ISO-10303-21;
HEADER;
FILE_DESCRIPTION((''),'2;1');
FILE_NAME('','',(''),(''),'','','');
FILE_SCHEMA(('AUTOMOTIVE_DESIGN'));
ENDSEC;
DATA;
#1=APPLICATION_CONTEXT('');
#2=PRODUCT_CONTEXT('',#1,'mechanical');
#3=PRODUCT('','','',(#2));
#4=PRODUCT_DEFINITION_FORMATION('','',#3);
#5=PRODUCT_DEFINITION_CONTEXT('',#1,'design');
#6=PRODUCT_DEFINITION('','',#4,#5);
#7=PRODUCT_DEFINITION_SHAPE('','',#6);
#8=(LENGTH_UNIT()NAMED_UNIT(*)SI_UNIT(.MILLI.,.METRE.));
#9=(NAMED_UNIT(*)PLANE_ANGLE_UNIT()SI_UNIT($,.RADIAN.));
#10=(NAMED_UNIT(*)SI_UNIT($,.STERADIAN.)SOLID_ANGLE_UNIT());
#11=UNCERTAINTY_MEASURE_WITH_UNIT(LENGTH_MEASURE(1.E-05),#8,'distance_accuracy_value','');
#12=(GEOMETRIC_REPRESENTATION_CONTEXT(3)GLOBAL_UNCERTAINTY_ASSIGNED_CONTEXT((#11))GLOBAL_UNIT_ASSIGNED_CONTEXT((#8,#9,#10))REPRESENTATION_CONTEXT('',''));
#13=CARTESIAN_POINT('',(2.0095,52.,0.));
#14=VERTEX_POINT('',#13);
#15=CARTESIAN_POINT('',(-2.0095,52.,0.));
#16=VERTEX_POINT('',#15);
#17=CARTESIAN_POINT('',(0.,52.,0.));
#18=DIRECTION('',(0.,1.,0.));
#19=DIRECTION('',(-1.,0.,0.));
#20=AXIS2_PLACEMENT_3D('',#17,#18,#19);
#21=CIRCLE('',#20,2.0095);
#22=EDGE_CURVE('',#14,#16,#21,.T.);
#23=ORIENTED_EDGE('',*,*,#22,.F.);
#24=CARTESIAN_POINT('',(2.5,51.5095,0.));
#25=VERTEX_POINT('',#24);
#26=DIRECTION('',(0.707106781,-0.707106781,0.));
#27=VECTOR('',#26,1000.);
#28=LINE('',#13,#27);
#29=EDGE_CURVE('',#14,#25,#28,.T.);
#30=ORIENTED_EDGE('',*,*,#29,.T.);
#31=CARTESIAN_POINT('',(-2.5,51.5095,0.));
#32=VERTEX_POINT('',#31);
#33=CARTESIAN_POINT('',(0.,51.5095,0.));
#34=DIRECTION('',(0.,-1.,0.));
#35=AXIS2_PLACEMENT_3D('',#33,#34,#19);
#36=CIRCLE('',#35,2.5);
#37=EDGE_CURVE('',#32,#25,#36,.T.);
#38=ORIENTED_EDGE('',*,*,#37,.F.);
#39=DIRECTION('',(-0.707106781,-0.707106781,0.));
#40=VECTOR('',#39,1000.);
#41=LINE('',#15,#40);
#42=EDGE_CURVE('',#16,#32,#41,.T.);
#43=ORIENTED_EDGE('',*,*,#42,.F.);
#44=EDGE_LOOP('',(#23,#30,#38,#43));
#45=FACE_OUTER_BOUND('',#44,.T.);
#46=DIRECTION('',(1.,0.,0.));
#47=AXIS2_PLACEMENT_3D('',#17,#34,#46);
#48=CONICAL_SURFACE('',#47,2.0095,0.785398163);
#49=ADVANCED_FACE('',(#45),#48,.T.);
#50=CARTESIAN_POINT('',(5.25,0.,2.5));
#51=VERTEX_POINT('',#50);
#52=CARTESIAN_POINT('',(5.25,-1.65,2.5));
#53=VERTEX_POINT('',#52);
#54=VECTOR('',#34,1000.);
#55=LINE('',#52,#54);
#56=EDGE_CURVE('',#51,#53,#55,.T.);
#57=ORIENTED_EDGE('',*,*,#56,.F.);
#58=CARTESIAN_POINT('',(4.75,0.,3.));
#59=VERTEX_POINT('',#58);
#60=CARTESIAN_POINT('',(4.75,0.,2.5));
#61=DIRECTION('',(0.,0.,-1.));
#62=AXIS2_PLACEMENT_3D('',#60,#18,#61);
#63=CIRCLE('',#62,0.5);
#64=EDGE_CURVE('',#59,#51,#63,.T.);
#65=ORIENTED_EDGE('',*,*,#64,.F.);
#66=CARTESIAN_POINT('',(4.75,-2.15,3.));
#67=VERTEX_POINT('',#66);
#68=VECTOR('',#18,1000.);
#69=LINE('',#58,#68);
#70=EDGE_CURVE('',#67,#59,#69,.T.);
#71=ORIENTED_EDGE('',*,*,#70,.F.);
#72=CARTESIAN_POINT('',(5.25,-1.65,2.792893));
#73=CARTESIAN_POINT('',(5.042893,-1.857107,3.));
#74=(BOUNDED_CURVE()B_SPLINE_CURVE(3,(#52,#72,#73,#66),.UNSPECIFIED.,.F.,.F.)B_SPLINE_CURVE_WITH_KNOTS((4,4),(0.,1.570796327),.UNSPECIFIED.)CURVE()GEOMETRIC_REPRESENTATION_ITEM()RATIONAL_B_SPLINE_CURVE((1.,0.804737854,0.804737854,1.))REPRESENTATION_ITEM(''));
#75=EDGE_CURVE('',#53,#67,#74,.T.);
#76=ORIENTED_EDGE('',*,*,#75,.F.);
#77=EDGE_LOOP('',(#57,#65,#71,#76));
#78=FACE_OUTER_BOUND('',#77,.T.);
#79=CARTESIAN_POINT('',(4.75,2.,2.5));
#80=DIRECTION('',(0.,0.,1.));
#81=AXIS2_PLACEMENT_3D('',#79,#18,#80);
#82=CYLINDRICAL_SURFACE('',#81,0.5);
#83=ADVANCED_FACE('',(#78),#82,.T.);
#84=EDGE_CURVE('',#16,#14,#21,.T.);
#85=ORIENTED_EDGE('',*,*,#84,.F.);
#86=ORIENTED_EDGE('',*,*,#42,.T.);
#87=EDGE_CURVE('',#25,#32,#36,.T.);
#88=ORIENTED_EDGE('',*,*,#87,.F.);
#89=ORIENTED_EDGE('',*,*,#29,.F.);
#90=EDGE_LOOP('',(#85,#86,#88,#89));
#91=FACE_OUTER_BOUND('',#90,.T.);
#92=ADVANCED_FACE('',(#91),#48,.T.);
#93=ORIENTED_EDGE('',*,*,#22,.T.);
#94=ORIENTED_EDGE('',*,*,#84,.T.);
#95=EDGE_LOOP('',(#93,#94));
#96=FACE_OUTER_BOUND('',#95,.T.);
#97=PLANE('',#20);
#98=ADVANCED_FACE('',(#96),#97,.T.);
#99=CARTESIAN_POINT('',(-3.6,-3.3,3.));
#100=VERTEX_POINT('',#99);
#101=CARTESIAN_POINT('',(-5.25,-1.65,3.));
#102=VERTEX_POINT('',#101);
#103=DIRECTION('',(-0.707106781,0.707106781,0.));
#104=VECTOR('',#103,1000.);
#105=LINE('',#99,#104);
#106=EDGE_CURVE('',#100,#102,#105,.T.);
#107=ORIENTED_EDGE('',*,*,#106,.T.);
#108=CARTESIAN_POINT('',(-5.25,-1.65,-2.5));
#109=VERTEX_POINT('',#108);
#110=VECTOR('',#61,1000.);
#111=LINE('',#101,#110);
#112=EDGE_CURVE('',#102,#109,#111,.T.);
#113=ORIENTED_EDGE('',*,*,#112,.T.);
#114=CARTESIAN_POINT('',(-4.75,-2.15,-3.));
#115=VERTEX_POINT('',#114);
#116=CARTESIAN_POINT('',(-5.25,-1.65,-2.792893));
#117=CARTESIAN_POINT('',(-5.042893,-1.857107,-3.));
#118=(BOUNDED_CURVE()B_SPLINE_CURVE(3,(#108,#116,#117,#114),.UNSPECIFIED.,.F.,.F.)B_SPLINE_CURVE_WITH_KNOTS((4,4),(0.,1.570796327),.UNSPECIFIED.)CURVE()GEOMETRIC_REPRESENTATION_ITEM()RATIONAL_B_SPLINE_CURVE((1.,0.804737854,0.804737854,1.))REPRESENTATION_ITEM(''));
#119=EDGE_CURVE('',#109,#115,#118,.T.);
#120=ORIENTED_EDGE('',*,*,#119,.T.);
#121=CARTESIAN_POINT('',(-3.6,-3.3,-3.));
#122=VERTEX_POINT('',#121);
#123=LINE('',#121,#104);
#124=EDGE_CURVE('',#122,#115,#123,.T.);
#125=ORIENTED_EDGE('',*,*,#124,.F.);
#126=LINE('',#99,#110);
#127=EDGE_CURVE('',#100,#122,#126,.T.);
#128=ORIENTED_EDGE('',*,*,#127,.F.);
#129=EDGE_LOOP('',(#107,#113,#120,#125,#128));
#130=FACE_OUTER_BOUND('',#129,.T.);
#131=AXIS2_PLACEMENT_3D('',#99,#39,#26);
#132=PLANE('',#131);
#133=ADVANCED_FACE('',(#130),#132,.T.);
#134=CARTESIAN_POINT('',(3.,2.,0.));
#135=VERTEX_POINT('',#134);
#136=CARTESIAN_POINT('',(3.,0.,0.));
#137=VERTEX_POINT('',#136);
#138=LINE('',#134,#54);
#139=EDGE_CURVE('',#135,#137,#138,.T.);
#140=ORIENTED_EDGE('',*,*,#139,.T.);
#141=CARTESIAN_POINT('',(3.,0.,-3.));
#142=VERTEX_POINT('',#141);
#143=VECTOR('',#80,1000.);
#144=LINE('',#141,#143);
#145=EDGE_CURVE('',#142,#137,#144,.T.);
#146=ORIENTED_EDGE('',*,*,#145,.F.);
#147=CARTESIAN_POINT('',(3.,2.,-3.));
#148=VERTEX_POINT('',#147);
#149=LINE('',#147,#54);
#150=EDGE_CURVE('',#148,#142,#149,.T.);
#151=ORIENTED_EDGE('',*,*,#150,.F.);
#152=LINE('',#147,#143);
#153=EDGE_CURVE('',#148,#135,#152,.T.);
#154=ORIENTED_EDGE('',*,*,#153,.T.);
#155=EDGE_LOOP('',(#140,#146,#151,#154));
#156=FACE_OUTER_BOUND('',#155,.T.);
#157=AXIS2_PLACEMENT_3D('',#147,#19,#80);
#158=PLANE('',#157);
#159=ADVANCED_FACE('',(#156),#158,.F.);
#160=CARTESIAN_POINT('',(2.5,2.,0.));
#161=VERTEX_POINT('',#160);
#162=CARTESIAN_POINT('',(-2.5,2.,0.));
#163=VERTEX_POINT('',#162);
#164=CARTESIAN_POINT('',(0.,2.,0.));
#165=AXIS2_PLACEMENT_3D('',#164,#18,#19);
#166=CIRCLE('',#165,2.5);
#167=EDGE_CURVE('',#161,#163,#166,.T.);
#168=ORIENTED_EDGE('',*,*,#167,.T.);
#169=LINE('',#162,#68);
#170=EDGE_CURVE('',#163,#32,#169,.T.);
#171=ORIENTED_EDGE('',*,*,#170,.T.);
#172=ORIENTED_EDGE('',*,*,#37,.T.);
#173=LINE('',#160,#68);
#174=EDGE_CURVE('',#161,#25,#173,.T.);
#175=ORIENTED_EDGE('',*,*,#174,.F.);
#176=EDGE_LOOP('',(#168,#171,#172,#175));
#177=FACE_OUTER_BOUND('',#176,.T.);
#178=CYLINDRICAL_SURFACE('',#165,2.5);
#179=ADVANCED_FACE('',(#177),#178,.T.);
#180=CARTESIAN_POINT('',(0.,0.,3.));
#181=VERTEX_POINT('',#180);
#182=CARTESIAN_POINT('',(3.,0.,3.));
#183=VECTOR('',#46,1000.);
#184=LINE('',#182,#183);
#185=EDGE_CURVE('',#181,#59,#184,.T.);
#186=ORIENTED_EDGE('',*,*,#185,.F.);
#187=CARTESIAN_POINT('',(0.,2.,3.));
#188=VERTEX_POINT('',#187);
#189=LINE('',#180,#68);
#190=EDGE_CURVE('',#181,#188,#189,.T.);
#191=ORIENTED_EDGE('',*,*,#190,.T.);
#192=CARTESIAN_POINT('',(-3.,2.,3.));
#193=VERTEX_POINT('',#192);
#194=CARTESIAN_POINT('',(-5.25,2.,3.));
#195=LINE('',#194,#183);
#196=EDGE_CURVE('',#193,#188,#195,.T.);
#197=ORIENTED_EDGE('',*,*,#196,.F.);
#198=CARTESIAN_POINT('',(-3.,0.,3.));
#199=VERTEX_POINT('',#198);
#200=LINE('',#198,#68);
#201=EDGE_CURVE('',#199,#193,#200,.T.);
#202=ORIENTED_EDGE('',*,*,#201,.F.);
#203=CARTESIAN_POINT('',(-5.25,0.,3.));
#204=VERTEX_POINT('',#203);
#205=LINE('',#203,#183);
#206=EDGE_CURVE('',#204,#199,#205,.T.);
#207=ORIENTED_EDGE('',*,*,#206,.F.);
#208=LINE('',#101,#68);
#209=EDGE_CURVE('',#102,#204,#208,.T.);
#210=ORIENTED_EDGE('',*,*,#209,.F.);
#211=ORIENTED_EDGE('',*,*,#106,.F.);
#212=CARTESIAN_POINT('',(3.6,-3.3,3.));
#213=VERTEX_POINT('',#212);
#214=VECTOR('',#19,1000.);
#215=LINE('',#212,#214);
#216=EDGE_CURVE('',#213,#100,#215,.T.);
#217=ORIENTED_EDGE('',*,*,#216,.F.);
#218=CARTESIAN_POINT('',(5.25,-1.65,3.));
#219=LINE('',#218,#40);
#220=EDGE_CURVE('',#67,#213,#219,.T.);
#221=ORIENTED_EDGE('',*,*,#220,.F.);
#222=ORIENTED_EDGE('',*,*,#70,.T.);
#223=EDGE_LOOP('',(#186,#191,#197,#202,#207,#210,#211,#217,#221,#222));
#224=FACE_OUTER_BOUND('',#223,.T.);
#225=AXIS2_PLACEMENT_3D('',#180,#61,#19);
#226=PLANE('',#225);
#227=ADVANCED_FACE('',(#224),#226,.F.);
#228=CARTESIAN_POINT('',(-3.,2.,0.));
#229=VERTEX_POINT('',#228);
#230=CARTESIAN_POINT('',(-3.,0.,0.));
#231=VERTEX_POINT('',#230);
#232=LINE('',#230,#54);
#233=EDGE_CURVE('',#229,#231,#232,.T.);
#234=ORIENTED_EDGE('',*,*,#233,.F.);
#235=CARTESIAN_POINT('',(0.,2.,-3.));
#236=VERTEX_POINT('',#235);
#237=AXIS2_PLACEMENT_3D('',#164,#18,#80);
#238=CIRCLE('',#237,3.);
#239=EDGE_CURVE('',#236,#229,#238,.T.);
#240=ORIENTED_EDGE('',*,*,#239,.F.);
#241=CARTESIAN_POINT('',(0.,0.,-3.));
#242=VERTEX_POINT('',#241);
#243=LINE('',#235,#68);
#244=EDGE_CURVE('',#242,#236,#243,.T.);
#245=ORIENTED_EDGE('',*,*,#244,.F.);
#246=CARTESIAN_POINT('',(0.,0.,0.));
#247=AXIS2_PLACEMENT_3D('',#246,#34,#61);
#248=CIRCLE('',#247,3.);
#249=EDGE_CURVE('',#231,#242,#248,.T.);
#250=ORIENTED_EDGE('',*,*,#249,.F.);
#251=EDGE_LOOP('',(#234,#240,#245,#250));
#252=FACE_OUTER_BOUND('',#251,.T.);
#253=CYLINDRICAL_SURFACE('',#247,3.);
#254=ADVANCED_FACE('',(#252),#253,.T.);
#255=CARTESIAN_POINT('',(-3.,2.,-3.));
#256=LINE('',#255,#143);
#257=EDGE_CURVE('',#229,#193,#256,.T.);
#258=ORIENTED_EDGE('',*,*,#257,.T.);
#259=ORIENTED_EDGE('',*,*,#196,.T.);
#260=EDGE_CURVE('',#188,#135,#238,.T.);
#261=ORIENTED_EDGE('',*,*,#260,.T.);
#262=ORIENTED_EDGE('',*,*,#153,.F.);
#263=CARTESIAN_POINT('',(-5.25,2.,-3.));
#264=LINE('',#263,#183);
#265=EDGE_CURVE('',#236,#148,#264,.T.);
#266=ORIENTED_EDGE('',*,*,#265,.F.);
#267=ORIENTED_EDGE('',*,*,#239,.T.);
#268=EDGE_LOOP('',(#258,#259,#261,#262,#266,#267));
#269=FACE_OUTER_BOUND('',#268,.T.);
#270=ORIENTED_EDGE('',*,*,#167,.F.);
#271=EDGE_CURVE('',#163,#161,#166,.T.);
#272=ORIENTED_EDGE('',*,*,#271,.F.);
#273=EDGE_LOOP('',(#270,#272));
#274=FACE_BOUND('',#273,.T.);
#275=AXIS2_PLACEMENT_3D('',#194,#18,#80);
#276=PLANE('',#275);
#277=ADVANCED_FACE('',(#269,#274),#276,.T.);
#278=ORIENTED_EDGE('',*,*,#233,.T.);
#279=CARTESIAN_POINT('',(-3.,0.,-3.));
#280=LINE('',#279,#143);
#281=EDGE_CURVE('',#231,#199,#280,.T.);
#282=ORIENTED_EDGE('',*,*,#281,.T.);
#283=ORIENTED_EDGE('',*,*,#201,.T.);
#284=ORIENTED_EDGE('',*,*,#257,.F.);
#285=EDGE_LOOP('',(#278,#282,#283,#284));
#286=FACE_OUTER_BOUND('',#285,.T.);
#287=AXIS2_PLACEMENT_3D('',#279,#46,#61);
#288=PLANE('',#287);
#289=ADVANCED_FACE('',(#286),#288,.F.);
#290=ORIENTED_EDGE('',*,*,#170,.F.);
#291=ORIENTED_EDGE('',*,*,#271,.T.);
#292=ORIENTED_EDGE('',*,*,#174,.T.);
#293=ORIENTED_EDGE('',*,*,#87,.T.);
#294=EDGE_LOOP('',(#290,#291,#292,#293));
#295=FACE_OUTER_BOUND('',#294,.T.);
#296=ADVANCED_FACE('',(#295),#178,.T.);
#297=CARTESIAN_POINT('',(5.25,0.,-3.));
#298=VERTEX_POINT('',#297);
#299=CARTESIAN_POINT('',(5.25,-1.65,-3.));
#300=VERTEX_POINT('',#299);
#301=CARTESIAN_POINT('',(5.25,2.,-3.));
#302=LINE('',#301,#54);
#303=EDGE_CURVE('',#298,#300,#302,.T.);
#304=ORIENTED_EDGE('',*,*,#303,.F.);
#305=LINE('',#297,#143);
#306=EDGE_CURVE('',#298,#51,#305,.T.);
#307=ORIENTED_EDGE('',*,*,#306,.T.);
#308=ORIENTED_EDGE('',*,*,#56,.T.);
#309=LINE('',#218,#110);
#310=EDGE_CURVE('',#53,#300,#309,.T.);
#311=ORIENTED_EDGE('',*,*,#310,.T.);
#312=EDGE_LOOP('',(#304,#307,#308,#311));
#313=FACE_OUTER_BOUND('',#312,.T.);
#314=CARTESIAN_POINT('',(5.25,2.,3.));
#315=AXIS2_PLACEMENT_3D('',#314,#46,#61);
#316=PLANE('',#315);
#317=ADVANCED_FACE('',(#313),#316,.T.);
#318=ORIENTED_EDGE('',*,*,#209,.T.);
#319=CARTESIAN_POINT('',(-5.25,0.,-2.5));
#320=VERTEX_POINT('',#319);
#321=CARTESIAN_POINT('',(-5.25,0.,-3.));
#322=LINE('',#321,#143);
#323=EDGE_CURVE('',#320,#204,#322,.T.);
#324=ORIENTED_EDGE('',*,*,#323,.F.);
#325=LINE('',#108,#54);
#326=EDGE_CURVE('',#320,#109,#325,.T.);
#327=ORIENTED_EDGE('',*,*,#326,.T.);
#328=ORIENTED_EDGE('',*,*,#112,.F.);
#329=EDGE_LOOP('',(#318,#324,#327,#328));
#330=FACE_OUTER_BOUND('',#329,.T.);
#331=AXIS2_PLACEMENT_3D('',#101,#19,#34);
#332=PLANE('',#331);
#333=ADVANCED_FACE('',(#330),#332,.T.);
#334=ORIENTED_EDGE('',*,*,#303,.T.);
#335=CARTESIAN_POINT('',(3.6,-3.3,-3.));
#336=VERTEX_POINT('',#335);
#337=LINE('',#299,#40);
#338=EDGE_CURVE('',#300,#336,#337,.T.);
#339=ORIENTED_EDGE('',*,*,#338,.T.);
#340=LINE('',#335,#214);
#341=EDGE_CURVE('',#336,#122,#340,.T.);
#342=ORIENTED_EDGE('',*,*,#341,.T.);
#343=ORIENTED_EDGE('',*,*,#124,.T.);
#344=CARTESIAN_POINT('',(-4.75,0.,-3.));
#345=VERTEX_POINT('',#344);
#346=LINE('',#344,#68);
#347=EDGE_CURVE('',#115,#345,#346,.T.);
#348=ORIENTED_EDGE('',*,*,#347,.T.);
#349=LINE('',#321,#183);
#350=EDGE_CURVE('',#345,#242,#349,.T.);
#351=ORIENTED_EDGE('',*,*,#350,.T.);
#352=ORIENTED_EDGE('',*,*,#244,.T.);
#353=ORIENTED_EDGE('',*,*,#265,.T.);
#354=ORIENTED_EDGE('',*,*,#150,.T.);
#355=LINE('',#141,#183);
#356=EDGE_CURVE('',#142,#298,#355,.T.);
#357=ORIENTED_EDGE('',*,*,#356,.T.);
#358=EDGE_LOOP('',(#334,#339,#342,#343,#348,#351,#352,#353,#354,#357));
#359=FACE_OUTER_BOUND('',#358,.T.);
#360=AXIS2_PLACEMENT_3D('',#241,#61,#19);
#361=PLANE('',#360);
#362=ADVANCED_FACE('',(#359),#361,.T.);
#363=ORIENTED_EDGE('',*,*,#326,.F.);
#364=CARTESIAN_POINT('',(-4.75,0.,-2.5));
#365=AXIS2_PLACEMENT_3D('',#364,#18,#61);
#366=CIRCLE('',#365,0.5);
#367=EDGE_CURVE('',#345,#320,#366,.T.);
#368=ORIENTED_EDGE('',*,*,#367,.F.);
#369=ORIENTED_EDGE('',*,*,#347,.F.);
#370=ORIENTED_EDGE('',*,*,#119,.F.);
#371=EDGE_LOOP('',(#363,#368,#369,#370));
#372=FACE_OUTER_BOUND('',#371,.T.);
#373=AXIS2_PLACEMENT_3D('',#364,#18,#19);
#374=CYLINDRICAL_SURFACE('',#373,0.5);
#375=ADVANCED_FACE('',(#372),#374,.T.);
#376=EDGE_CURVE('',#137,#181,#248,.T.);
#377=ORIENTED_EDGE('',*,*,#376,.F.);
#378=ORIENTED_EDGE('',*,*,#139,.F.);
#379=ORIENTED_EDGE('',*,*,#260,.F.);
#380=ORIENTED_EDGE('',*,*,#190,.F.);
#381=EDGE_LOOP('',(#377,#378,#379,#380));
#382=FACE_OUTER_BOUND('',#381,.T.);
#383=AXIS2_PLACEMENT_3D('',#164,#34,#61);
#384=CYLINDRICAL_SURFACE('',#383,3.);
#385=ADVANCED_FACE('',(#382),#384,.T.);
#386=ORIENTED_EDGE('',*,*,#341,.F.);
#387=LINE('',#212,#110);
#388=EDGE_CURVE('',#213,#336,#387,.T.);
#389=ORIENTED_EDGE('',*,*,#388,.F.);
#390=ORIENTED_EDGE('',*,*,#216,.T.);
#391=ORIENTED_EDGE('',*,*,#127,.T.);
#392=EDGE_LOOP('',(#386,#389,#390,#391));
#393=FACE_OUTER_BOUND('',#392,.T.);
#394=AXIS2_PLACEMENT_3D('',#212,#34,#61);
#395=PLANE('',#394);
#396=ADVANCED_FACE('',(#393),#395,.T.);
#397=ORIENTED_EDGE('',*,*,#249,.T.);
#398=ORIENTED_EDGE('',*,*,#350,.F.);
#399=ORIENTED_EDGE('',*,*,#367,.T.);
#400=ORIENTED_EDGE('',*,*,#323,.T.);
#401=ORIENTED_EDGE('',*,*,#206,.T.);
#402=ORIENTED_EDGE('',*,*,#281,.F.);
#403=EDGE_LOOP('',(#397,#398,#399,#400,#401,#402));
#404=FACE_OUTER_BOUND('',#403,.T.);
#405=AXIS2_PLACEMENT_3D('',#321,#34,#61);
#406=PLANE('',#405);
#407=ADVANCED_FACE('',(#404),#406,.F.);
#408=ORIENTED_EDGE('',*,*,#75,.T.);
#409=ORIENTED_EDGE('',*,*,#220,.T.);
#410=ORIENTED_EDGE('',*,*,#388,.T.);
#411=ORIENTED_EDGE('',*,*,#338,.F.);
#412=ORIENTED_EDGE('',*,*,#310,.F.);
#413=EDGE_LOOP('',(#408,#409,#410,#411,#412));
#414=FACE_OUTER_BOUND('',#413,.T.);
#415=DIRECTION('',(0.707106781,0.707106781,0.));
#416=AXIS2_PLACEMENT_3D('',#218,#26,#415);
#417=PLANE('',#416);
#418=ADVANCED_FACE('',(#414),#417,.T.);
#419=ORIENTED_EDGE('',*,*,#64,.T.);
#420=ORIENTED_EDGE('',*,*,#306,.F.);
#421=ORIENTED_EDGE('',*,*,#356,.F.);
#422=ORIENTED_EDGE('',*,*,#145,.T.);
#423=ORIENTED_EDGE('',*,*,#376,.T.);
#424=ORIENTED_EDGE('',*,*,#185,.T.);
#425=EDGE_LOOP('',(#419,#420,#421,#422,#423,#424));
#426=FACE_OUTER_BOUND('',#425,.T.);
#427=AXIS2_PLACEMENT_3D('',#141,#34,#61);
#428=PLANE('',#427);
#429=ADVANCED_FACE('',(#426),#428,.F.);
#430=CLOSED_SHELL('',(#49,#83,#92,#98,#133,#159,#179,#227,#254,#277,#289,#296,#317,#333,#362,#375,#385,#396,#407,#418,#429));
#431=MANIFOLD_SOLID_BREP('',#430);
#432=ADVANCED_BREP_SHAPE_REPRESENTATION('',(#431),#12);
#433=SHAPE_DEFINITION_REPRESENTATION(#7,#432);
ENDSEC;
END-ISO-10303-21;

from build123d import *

# Parameters (mm, degrees)
BOSS_EXTRUDE1_DEPTH = 6
SKETCH2_W           = 2.25
SKETCH2_H           = 2
CUT_EXTRUDE1_DEPTH  = 9.628586211
SKETCH3_W           = 2.25
SKETCH3_H           = 2
CUT_EXTRUDE2_DEPTH  = 9.628586211
SKETCH4_W           = 2.5
SKETCH4_H           = 50
CHAMFER1_SIZE       = 0.4905
FILLET1_R           = 0.5
FILLET2_R           = 3


with BuildPart() as part:
    # Sketch1 → Boss-Extrude1 (new body)
    with BuildSketch(Plane(origin=(0, 0, -3), x_dir=(-1, 0, 0), z_dir=(0, 0, -1))):
        Polygon((5.25, 2), (-5.25, 2), (-5.25, -1.65), (-3.6, -3.3), (3.6, -3.3), (5.25, -1.65), align=None)
    extrude(amount=-BOSS_EXTRUDE1_DEPTH)

    # Sketch2 → Cut-Extrude1 (cut, through all)
    with BuildSketch(Plane.XY.offset(3)):
        with Locations((-4.125, 1)):
            Rectangle(SKETCH2_W, SKETCH2_H)
    extrude(amount=-CUT_EXTRUDE1_DEPTH, mode=Mode.SUBTRACT)

    # Sketch3 → Cut-Extrude2 (cut, through all)
    with BuildSketch(Plane.XY.offset(3)):
        with Locations((4.125, 1)):
            Rectangle(SKETCH3_W, SKETCH3_H)
    extrude(amount=-CUT_EXTRUDE2_DEPTH, mode=Mode.SUBTRACT)

    # Sketch4 → Revolve1 (revolve)
    with BuildSketch(Plane(origin=(0, 0, 0), x_dir=(-1, 0, 0), z_dir=(0, 0, -1)), mode=Mode.PRIVATE) as revolve1_sk:
        with Locations((-1.25, 27)):
            Rectangle(SKETCH4_W, SKETCH4_H)
    revolve(revolve1_sk.sketch.rotate(Axis((0, 2, 0), (0, 1, 0)), 180), axis=Axis((0, 2, 0), (0, 1, 0)))

    # Chamfer1
    chamfer1_edges = [part.edges().sort_by_distance(p)[0] for p in [
        (2.5, 52, 0),
    ]]
    chamfer(chamfer1_edges, length=CHAMFER1_SIZE)

    # Fillet1
    fillet1_edges = [part.edges().sort_by_distance(p)[0] for p in [
        (5.25, -0.825, 3),
        (-5.25, -0.825, -3),
    ]]
    fillet(fillet1_edges, radius=FILLET1_R)

    # Fillet2
    fillet2_edges = [part.edges().sort_by_distance(p)[0] for p in [
        (-3, 1, -3),
        (3, 1, 3),
    ]]
    fillet(fillet2_edges, radius=FILLET2_R)


solid = part.part
